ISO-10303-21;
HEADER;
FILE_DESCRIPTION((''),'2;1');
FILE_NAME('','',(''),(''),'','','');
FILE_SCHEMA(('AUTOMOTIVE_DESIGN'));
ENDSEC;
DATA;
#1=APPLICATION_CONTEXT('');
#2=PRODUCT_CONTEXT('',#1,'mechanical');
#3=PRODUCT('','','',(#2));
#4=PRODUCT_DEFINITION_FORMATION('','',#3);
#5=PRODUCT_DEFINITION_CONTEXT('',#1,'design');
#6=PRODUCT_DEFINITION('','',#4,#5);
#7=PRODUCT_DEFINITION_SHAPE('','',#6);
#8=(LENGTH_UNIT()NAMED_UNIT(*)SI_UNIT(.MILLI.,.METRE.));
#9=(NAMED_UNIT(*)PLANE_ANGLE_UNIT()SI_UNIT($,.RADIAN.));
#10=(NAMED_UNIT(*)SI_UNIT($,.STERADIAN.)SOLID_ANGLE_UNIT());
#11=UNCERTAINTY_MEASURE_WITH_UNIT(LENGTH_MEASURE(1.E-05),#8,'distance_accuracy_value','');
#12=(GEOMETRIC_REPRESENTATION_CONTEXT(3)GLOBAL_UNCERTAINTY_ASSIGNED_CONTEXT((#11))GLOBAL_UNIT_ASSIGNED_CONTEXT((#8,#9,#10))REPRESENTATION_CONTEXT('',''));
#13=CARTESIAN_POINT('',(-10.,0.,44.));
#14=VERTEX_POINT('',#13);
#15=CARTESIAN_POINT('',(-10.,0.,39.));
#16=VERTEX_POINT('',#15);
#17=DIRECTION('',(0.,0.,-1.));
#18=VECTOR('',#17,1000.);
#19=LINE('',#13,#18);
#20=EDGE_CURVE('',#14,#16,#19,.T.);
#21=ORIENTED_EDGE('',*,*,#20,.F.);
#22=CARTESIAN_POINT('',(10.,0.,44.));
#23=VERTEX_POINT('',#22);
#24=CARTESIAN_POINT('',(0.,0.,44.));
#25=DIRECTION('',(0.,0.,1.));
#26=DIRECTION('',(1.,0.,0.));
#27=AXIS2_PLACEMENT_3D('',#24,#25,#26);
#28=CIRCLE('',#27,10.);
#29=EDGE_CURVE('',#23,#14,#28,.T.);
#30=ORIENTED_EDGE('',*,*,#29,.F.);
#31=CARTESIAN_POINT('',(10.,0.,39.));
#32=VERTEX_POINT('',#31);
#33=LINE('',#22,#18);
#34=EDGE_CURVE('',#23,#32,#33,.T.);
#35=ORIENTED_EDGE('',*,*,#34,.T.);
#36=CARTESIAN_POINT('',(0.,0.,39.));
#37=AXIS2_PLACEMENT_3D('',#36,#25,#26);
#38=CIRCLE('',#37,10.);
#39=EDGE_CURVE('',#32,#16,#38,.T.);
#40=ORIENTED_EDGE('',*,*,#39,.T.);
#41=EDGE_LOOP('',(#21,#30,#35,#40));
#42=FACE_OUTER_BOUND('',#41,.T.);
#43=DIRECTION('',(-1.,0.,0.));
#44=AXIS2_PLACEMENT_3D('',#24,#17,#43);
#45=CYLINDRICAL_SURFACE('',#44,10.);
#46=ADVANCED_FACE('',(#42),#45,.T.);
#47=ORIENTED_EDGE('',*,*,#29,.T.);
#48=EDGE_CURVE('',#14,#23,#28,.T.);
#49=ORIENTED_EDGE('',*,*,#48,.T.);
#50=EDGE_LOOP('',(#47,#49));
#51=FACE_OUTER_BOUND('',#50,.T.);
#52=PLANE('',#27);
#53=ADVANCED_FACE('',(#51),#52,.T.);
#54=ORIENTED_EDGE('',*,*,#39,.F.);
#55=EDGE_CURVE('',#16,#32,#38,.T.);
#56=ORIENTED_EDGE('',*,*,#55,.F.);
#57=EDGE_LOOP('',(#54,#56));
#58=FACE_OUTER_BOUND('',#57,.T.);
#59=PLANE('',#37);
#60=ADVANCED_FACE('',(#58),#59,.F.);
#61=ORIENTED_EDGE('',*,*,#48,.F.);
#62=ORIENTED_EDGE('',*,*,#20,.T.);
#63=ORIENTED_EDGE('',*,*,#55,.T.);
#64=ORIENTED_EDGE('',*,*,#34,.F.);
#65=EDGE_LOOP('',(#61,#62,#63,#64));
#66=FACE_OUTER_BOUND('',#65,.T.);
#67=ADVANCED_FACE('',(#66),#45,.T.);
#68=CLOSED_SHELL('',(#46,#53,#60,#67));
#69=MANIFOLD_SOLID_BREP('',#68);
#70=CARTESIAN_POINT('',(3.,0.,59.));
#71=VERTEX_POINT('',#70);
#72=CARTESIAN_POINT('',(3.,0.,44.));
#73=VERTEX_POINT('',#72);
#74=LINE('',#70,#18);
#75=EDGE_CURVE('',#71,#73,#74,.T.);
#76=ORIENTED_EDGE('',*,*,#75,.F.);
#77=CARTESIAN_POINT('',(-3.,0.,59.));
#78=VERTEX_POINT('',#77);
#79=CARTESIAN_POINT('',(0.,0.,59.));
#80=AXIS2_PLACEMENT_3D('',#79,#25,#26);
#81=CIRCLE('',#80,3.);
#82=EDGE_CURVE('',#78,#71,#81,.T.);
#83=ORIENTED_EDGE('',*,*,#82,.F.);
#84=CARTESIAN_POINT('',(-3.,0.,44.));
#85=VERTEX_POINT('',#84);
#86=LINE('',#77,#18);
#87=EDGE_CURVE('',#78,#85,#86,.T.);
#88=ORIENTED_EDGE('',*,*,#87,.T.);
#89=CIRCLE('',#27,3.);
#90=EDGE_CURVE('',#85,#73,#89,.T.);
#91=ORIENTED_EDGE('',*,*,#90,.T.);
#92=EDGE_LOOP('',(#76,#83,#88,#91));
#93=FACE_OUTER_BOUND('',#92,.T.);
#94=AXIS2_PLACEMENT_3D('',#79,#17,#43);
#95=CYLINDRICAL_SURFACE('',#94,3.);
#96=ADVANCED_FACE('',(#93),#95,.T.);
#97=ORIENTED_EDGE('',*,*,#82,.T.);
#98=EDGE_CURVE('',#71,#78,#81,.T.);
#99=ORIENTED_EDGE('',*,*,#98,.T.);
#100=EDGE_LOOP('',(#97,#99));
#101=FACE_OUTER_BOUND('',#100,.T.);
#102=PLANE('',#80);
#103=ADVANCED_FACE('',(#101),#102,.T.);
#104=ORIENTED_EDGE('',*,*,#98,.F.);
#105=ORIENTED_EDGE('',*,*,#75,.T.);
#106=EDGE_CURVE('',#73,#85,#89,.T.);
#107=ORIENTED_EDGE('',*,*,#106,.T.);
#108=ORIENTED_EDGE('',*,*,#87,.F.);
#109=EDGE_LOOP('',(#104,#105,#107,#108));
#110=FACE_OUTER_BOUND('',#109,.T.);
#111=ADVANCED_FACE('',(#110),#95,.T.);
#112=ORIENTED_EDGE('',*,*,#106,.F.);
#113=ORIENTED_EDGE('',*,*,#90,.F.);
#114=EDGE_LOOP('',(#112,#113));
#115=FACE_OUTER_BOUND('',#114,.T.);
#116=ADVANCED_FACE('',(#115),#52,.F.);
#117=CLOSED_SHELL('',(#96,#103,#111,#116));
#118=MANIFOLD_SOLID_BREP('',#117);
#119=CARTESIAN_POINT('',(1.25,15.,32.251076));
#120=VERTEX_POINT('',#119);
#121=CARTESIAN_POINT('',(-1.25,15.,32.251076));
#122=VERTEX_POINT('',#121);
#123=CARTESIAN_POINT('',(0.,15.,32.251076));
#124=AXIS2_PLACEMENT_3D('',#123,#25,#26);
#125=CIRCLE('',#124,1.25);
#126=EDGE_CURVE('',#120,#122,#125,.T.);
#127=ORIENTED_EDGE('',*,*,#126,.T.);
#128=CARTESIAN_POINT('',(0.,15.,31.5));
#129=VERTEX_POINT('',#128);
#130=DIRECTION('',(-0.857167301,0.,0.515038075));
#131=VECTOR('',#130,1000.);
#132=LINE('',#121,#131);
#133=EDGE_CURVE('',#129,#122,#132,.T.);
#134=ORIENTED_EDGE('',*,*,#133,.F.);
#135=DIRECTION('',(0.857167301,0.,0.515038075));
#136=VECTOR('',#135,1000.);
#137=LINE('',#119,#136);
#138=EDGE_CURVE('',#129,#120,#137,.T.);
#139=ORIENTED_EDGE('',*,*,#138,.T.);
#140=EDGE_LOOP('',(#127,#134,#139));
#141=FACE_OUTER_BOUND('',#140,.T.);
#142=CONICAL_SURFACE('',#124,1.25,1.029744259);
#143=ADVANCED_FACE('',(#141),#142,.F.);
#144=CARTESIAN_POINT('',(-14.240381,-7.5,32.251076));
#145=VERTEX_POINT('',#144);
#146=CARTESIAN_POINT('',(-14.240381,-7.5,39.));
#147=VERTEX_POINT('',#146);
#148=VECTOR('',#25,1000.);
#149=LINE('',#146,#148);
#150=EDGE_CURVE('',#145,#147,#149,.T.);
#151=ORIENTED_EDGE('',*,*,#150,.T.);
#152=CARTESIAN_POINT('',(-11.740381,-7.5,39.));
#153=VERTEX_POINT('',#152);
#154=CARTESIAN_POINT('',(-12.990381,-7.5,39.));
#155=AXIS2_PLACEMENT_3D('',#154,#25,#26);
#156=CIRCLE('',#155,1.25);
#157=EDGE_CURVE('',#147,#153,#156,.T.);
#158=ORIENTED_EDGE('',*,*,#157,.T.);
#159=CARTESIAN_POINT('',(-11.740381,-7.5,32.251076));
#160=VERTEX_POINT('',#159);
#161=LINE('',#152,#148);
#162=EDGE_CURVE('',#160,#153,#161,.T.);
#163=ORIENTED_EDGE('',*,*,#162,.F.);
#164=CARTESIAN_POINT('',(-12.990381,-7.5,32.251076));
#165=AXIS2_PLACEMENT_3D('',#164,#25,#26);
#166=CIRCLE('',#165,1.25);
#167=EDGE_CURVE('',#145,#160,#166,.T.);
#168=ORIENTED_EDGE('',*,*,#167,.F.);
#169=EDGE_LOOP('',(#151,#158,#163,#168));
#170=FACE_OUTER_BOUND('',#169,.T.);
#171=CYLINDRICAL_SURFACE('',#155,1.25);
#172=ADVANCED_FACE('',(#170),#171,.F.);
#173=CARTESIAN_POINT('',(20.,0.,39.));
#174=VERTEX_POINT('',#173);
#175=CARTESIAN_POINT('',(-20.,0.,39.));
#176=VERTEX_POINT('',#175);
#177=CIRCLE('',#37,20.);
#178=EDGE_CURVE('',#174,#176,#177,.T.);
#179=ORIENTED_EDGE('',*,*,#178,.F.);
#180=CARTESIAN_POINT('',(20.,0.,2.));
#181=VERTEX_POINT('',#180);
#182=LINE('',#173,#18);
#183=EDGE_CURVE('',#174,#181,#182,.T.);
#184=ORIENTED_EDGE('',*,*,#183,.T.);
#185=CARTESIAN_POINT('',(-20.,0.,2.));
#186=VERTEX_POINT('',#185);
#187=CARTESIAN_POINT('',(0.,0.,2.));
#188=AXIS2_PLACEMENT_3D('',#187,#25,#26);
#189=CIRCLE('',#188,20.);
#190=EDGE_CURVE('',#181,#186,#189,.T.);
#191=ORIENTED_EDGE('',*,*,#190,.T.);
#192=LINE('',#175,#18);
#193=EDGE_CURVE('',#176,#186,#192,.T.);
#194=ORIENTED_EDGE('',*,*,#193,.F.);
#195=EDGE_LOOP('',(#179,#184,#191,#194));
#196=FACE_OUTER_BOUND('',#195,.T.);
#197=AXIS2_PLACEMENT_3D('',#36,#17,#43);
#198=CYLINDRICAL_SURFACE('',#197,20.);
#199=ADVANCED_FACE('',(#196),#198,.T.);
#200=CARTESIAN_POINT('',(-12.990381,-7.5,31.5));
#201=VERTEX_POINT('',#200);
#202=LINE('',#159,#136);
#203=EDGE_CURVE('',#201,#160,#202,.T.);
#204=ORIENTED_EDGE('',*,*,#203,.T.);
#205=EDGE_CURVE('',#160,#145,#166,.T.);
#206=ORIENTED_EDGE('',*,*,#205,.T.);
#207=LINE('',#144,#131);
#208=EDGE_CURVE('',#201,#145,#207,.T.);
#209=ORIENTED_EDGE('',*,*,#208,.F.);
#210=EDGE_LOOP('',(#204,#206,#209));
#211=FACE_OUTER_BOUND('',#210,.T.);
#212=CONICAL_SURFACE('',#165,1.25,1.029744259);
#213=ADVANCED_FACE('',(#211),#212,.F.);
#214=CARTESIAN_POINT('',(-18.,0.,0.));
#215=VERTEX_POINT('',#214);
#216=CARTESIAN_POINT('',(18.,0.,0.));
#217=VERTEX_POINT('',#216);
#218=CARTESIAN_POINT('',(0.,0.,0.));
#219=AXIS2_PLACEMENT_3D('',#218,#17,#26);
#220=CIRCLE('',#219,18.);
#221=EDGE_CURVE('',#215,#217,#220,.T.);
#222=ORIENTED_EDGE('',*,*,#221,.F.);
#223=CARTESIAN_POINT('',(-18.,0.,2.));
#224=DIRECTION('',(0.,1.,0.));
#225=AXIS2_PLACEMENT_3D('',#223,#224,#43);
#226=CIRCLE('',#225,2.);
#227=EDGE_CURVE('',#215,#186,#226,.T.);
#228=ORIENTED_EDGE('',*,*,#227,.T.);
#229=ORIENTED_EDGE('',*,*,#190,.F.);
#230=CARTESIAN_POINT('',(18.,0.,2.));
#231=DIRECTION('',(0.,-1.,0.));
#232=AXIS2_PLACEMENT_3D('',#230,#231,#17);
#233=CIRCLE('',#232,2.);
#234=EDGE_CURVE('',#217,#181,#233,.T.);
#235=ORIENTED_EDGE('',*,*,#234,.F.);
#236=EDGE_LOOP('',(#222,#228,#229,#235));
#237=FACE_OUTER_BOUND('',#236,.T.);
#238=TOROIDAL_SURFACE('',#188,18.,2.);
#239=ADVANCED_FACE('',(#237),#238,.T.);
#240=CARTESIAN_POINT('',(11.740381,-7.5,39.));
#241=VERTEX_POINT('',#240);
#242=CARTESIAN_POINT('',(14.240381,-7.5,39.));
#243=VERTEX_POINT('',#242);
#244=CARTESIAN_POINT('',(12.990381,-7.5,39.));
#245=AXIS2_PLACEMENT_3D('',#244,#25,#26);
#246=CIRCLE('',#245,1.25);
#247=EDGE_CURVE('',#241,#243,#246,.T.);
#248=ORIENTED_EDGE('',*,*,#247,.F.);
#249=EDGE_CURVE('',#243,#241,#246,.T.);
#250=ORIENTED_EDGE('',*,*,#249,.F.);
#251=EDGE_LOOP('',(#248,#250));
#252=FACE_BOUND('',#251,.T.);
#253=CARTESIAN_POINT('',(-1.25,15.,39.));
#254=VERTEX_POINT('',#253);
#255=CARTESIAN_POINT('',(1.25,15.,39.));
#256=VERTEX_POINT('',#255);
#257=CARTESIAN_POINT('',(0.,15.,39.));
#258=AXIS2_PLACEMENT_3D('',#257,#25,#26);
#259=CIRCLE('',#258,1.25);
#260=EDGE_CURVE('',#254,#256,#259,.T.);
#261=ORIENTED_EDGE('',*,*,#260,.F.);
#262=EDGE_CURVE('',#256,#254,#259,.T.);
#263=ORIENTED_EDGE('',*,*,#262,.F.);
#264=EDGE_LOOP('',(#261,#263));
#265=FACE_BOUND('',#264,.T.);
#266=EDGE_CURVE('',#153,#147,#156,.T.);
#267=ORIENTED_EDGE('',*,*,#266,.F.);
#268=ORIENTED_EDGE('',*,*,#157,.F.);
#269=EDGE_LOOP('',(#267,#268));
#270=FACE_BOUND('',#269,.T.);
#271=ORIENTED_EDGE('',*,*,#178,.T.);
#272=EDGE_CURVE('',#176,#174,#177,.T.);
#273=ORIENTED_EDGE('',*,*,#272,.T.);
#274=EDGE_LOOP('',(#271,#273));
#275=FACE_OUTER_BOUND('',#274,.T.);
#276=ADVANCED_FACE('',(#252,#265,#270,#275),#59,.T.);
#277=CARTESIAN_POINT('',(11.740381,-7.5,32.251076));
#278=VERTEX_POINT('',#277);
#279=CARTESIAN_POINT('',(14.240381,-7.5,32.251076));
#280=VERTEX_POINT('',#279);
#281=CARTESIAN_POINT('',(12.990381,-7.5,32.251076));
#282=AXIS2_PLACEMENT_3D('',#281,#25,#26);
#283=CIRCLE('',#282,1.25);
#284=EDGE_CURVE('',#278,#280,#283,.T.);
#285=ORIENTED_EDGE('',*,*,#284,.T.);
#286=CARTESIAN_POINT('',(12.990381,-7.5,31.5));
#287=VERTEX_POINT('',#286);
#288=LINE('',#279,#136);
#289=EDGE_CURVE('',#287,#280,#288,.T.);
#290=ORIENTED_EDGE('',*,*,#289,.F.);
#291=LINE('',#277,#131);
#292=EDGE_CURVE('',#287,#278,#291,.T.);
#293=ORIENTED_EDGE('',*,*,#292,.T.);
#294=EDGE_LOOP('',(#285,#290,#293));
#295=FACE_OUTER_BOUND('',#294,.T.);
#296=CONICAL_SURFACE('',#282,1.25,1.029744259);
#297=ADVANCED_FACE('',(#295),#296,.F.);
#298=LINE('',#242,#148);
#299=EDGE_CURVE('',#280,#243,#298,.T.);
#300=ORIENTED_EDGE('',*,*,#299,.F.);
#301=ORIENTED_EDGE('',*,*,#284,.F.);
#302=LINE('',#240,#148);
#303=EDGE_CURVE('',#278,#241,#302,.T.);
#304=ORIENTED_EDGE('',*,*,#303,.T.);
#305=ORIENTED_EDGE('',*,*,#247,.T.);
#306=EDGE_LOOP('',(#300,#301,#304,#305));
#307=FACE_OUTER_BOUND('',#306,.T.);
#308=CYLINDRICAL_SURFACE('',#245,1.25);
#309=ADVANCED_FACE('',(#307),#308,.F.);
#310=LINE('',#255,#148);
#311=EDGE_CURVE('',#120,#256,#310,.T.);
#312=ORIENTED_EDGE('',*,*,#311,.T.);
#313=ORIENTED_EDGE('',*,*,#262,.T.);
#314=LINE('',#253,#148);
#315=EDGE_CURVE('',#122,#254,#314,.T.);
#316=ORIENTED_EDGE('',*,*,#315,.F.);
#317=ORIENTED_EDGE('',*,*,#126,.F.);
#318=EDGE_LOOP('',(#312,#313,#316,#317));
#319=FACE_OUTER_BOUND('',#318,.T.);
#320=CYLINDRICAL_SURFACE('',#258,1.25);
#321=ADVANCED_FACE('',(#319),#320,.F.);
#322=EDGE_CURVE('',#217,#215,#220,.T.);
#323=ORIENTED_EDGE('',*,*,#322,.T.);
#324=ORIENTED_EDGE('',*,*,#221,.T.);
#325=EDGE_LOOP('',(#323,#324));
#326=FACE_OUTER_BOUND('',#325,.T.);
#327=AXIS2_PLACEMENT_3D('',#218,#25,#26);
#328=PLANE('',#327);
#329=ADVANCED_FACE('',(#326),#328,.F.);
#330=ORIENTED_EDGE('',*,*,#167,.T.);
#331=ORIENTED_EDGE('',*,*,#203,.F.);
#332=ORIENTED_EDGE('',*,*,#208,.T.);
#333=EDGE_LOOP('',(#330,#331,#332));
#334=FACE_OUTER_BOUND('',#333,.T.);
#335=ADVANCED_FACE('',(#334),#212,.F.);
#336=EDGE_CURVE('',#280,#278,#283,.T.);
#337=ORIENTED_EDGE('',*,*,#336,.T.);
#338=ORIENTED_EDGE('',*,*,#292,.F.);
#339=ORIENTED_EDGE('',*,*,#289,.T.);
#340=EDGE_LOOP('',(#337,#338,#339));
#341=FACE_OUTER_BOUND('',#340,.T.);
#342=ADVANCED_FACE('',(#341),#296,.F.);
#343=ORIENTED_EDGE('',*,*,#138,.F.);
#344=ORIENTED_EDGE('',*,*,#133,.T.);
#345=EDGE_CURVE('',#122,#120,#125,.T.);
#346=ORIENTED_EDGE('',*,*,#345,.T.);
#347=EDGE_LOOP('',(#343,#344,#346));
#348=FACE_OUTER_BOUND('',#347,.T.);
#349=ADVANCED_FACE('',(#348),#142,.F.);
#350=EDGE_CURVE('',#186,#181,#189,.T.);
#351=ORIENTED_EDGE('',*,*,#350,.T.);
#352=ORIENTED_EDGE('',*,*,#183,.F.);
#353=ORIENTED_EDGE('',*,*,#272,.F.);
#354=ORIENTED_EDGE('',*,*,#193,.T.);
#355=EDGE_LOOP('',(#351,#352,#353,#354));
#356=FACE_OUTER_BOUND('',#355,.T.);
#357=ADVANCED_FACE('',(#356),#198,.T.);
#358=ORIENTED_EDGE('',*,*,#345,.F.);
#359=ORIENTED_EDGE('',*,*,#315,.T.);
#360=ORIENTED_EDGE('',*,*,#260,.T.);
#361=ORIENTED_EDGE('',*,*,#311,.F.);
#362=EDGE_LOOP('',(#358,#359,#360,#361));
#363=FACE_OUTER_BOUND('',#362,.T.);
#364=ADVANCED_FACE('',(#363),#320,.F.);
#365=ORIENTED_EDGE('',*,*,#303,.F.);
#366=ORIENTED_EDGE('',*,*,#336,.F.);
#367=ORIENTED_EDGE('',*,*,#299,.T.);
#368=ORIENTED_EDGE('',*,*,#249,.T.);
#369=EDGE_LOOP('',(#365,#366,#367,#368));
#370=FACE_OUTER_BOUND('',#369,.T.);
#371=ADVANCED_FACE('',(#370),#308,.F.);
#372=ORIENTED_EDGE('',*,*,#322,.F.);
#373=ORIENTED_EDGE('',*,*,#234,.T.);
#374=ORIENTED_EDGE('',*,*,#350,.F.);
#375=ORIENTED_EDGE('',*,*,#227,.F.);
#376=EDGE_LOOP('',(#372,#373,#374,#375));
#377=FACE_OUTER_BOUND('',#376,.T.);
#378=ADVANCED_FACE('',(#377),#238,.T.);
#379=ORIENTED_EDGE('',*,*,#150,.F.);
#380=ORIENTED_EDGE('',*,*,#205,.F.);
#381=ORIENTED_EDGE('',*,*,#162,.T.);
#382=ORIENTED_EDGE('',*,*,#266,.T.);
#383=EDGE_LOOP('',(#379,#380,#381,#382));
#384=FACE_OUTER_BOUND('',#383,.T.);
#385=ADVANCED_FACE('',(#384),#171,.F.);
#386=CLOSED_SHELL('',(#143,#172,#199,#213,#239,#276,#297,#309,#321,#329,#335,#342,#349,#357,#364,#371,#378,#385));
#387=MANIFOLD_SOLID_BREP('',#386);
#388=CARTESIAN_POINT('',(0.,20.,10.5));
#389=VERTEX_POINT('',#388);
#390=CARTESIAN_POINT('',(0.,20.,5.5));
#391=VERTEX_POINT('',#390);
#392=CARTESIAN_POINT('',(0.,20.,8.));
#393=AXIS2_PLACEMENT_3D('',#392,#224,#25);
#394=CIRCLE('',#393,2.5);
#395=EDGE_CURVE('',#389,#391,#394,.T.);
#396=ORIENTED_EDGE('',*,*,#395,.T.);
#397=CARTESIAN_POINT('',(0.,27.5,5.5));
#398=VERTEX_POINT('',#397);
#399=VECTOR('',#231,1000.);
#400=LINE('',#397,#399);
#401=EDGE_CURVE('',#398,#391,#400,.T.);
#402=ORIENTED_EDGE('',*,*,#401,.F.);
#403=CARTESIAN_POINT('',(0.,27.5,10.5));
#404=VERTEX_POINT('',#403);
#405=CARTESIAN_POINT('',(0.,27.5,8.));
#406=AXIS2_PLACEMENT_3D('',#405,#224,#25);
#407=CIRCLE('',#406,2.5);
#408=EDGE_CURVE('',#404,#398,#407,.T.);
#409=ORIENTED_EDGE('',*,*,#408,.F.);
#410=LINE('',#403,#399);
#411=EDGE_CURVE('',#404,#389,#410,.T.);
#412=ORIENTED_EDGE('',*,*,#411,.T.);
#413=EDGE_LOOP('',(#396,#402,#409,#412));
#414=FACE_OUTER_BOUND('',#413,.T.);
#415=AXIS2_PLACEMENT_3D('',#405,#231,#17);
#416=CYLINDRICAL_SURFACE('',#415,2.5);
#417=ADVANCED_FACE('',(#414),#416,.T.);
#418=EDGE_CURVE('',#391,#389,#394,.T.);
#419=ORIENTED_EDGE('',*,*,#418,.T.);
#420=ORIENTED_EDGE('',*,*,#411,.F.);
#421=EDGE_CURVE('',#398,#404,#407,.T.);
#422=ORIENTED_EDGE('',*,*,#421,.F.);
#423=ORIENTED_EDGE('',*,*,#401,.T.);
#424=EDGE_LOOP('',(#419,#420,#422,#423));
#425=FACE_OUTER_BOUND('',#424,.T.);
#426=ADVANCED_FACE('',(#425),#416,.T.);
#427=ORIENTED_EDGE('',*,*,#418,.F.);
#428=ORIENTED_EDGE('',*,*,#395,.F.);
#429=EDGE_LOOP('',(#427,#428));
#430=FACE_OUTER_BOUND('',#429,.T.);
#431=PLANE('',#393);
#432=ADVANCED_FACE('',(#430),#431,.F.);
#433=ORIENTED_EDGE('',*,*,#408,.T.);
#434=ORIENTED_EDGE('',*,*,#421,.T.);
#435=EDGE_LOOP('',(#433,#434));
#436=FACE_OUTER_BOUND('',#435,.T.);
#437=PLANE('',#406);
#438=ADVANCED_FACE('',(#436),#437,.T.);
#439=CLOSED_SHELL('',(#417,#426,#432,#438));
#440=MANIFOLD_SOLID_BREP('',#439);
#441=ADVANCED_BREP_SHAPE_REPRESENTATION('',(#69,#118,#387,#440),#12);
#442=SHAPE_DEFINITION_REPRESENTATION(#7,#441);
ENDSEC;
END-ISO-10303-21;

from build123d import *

# Parameters (mm, degrees)
SKETCH_1_R                  = 20
EXTRUDE_1_DEPTH             = 39
SKETCH_2_R                  = 10
EXTRUDE_2_DEPTH             = 5
SKETCH_3_R                  = 3
EXTRUDE_3_DEPTH             = 15
HOLE_WIZARD_M3_1_AT_2_COUNT = 2
HOLE_WIZARD_M3_1_AT_2_PITCH = 25.980762114
HOLE_WIZARD_M3_1_AT_3_COUNT = 2
HOLE_WIZARD_M3_1_AT_3_PITCH = 25.980762114
FILLET_1_R                  = 2
SKETCH_8_R                  = 2.5
EXTRUDE_4_DEPTH             = 7.5


with BuildPart() as part:
    # 草图1 → 凸台-拉伸1 (new body)
    with BuildSketch(Plane.XY):
        Circle(SKETCH_1_R)
    extrude(amount=EXTRUDE_1_DEPTH)

    # 草图6 → M3 螺纹孔1 (revolve, cut)
    with BuildSketch(Plane(origin=(0, 15, 39), x_dir=(0, -1, 0), z_dir=(1, 0, 0))):
        Polygon((0, 0), (0, 7.5), (1.25, 6.748924226), (1.25, 0), align=None)
    hole_wizard_m3_1 = revolve(axis=Axis((0, 15, 45.35), (0, 0, -1)), mode=Mode.SUBTRACT)

    # M3 螺纹孔1 at 2: M3 螺纹孔1 ×2
    with Locations(*[Vector(-0.49999999999996314, -0.8660254037844599, 0) * (i * HOLE_WIZARD_M3_1_AT_2_PITCH) for i in range(1, HOLE_WIZARD_M3_1_AT_2_COUNT)]):
        add(hole_wizard_m3_1, mode=Mode.SUBTRACT)

    # M3 螺纹孔1 at 3: M3 螺纹孔1 ×2
    with Locations(*[Vector(0.5000000000000372, -0.8660254037844173, 0) * (i * HOLE_WIZARD_M3_1_AT_3_PITCH) for i in range(1, HOLE_WIZARD_M3_1_AT_3_COUNT)]):
        add(hole_wizard_m3_1, mode=Mode.SUBTRACT)

    # 圆角1
    fillet_1_edges = [part.edges().sort_by_distance(p)[0] for p in [
        (-20, 0, 0),
    ]]
    fillet(fillet_1_edges, radius=FILLET_1_R)


with BuildPart() as body_2:
    # 草图2 → 凸台-拉伸2 (new body)
    with BuildSketch(Plane.XY.offset(39)):
        Circle(SKETCH_2_R)
    extrude(amount=EXTRUDE_2_DEPTH)


with BuildPart() as body_3:
    # 草图3 → 凸台-拉伸3 (new body)
    with BuildSketch(Plane.XY.offset(44)):
        Circle(SKETCH_3_R)
    extrude(amount=EXTRUDE_3_DEPTH)


with BuildPart() as body_4:
    # 草图8 → 凸台-拉伸4 (new body)
    with BuildSketch(Plane(origin=(0, 20, 0), x_dir=(1, 0, 0), z_dir=(0, 1, 0))):
        with Locations(Location((0, -8, 0), (0, 0, 270))):
            Circle(SKETCH_8_R)
    extrude(amount=EXTRUDE_4_DEPTH)


solid = Compound([part.part, body_2.part, body_3.part, body_4.part])
